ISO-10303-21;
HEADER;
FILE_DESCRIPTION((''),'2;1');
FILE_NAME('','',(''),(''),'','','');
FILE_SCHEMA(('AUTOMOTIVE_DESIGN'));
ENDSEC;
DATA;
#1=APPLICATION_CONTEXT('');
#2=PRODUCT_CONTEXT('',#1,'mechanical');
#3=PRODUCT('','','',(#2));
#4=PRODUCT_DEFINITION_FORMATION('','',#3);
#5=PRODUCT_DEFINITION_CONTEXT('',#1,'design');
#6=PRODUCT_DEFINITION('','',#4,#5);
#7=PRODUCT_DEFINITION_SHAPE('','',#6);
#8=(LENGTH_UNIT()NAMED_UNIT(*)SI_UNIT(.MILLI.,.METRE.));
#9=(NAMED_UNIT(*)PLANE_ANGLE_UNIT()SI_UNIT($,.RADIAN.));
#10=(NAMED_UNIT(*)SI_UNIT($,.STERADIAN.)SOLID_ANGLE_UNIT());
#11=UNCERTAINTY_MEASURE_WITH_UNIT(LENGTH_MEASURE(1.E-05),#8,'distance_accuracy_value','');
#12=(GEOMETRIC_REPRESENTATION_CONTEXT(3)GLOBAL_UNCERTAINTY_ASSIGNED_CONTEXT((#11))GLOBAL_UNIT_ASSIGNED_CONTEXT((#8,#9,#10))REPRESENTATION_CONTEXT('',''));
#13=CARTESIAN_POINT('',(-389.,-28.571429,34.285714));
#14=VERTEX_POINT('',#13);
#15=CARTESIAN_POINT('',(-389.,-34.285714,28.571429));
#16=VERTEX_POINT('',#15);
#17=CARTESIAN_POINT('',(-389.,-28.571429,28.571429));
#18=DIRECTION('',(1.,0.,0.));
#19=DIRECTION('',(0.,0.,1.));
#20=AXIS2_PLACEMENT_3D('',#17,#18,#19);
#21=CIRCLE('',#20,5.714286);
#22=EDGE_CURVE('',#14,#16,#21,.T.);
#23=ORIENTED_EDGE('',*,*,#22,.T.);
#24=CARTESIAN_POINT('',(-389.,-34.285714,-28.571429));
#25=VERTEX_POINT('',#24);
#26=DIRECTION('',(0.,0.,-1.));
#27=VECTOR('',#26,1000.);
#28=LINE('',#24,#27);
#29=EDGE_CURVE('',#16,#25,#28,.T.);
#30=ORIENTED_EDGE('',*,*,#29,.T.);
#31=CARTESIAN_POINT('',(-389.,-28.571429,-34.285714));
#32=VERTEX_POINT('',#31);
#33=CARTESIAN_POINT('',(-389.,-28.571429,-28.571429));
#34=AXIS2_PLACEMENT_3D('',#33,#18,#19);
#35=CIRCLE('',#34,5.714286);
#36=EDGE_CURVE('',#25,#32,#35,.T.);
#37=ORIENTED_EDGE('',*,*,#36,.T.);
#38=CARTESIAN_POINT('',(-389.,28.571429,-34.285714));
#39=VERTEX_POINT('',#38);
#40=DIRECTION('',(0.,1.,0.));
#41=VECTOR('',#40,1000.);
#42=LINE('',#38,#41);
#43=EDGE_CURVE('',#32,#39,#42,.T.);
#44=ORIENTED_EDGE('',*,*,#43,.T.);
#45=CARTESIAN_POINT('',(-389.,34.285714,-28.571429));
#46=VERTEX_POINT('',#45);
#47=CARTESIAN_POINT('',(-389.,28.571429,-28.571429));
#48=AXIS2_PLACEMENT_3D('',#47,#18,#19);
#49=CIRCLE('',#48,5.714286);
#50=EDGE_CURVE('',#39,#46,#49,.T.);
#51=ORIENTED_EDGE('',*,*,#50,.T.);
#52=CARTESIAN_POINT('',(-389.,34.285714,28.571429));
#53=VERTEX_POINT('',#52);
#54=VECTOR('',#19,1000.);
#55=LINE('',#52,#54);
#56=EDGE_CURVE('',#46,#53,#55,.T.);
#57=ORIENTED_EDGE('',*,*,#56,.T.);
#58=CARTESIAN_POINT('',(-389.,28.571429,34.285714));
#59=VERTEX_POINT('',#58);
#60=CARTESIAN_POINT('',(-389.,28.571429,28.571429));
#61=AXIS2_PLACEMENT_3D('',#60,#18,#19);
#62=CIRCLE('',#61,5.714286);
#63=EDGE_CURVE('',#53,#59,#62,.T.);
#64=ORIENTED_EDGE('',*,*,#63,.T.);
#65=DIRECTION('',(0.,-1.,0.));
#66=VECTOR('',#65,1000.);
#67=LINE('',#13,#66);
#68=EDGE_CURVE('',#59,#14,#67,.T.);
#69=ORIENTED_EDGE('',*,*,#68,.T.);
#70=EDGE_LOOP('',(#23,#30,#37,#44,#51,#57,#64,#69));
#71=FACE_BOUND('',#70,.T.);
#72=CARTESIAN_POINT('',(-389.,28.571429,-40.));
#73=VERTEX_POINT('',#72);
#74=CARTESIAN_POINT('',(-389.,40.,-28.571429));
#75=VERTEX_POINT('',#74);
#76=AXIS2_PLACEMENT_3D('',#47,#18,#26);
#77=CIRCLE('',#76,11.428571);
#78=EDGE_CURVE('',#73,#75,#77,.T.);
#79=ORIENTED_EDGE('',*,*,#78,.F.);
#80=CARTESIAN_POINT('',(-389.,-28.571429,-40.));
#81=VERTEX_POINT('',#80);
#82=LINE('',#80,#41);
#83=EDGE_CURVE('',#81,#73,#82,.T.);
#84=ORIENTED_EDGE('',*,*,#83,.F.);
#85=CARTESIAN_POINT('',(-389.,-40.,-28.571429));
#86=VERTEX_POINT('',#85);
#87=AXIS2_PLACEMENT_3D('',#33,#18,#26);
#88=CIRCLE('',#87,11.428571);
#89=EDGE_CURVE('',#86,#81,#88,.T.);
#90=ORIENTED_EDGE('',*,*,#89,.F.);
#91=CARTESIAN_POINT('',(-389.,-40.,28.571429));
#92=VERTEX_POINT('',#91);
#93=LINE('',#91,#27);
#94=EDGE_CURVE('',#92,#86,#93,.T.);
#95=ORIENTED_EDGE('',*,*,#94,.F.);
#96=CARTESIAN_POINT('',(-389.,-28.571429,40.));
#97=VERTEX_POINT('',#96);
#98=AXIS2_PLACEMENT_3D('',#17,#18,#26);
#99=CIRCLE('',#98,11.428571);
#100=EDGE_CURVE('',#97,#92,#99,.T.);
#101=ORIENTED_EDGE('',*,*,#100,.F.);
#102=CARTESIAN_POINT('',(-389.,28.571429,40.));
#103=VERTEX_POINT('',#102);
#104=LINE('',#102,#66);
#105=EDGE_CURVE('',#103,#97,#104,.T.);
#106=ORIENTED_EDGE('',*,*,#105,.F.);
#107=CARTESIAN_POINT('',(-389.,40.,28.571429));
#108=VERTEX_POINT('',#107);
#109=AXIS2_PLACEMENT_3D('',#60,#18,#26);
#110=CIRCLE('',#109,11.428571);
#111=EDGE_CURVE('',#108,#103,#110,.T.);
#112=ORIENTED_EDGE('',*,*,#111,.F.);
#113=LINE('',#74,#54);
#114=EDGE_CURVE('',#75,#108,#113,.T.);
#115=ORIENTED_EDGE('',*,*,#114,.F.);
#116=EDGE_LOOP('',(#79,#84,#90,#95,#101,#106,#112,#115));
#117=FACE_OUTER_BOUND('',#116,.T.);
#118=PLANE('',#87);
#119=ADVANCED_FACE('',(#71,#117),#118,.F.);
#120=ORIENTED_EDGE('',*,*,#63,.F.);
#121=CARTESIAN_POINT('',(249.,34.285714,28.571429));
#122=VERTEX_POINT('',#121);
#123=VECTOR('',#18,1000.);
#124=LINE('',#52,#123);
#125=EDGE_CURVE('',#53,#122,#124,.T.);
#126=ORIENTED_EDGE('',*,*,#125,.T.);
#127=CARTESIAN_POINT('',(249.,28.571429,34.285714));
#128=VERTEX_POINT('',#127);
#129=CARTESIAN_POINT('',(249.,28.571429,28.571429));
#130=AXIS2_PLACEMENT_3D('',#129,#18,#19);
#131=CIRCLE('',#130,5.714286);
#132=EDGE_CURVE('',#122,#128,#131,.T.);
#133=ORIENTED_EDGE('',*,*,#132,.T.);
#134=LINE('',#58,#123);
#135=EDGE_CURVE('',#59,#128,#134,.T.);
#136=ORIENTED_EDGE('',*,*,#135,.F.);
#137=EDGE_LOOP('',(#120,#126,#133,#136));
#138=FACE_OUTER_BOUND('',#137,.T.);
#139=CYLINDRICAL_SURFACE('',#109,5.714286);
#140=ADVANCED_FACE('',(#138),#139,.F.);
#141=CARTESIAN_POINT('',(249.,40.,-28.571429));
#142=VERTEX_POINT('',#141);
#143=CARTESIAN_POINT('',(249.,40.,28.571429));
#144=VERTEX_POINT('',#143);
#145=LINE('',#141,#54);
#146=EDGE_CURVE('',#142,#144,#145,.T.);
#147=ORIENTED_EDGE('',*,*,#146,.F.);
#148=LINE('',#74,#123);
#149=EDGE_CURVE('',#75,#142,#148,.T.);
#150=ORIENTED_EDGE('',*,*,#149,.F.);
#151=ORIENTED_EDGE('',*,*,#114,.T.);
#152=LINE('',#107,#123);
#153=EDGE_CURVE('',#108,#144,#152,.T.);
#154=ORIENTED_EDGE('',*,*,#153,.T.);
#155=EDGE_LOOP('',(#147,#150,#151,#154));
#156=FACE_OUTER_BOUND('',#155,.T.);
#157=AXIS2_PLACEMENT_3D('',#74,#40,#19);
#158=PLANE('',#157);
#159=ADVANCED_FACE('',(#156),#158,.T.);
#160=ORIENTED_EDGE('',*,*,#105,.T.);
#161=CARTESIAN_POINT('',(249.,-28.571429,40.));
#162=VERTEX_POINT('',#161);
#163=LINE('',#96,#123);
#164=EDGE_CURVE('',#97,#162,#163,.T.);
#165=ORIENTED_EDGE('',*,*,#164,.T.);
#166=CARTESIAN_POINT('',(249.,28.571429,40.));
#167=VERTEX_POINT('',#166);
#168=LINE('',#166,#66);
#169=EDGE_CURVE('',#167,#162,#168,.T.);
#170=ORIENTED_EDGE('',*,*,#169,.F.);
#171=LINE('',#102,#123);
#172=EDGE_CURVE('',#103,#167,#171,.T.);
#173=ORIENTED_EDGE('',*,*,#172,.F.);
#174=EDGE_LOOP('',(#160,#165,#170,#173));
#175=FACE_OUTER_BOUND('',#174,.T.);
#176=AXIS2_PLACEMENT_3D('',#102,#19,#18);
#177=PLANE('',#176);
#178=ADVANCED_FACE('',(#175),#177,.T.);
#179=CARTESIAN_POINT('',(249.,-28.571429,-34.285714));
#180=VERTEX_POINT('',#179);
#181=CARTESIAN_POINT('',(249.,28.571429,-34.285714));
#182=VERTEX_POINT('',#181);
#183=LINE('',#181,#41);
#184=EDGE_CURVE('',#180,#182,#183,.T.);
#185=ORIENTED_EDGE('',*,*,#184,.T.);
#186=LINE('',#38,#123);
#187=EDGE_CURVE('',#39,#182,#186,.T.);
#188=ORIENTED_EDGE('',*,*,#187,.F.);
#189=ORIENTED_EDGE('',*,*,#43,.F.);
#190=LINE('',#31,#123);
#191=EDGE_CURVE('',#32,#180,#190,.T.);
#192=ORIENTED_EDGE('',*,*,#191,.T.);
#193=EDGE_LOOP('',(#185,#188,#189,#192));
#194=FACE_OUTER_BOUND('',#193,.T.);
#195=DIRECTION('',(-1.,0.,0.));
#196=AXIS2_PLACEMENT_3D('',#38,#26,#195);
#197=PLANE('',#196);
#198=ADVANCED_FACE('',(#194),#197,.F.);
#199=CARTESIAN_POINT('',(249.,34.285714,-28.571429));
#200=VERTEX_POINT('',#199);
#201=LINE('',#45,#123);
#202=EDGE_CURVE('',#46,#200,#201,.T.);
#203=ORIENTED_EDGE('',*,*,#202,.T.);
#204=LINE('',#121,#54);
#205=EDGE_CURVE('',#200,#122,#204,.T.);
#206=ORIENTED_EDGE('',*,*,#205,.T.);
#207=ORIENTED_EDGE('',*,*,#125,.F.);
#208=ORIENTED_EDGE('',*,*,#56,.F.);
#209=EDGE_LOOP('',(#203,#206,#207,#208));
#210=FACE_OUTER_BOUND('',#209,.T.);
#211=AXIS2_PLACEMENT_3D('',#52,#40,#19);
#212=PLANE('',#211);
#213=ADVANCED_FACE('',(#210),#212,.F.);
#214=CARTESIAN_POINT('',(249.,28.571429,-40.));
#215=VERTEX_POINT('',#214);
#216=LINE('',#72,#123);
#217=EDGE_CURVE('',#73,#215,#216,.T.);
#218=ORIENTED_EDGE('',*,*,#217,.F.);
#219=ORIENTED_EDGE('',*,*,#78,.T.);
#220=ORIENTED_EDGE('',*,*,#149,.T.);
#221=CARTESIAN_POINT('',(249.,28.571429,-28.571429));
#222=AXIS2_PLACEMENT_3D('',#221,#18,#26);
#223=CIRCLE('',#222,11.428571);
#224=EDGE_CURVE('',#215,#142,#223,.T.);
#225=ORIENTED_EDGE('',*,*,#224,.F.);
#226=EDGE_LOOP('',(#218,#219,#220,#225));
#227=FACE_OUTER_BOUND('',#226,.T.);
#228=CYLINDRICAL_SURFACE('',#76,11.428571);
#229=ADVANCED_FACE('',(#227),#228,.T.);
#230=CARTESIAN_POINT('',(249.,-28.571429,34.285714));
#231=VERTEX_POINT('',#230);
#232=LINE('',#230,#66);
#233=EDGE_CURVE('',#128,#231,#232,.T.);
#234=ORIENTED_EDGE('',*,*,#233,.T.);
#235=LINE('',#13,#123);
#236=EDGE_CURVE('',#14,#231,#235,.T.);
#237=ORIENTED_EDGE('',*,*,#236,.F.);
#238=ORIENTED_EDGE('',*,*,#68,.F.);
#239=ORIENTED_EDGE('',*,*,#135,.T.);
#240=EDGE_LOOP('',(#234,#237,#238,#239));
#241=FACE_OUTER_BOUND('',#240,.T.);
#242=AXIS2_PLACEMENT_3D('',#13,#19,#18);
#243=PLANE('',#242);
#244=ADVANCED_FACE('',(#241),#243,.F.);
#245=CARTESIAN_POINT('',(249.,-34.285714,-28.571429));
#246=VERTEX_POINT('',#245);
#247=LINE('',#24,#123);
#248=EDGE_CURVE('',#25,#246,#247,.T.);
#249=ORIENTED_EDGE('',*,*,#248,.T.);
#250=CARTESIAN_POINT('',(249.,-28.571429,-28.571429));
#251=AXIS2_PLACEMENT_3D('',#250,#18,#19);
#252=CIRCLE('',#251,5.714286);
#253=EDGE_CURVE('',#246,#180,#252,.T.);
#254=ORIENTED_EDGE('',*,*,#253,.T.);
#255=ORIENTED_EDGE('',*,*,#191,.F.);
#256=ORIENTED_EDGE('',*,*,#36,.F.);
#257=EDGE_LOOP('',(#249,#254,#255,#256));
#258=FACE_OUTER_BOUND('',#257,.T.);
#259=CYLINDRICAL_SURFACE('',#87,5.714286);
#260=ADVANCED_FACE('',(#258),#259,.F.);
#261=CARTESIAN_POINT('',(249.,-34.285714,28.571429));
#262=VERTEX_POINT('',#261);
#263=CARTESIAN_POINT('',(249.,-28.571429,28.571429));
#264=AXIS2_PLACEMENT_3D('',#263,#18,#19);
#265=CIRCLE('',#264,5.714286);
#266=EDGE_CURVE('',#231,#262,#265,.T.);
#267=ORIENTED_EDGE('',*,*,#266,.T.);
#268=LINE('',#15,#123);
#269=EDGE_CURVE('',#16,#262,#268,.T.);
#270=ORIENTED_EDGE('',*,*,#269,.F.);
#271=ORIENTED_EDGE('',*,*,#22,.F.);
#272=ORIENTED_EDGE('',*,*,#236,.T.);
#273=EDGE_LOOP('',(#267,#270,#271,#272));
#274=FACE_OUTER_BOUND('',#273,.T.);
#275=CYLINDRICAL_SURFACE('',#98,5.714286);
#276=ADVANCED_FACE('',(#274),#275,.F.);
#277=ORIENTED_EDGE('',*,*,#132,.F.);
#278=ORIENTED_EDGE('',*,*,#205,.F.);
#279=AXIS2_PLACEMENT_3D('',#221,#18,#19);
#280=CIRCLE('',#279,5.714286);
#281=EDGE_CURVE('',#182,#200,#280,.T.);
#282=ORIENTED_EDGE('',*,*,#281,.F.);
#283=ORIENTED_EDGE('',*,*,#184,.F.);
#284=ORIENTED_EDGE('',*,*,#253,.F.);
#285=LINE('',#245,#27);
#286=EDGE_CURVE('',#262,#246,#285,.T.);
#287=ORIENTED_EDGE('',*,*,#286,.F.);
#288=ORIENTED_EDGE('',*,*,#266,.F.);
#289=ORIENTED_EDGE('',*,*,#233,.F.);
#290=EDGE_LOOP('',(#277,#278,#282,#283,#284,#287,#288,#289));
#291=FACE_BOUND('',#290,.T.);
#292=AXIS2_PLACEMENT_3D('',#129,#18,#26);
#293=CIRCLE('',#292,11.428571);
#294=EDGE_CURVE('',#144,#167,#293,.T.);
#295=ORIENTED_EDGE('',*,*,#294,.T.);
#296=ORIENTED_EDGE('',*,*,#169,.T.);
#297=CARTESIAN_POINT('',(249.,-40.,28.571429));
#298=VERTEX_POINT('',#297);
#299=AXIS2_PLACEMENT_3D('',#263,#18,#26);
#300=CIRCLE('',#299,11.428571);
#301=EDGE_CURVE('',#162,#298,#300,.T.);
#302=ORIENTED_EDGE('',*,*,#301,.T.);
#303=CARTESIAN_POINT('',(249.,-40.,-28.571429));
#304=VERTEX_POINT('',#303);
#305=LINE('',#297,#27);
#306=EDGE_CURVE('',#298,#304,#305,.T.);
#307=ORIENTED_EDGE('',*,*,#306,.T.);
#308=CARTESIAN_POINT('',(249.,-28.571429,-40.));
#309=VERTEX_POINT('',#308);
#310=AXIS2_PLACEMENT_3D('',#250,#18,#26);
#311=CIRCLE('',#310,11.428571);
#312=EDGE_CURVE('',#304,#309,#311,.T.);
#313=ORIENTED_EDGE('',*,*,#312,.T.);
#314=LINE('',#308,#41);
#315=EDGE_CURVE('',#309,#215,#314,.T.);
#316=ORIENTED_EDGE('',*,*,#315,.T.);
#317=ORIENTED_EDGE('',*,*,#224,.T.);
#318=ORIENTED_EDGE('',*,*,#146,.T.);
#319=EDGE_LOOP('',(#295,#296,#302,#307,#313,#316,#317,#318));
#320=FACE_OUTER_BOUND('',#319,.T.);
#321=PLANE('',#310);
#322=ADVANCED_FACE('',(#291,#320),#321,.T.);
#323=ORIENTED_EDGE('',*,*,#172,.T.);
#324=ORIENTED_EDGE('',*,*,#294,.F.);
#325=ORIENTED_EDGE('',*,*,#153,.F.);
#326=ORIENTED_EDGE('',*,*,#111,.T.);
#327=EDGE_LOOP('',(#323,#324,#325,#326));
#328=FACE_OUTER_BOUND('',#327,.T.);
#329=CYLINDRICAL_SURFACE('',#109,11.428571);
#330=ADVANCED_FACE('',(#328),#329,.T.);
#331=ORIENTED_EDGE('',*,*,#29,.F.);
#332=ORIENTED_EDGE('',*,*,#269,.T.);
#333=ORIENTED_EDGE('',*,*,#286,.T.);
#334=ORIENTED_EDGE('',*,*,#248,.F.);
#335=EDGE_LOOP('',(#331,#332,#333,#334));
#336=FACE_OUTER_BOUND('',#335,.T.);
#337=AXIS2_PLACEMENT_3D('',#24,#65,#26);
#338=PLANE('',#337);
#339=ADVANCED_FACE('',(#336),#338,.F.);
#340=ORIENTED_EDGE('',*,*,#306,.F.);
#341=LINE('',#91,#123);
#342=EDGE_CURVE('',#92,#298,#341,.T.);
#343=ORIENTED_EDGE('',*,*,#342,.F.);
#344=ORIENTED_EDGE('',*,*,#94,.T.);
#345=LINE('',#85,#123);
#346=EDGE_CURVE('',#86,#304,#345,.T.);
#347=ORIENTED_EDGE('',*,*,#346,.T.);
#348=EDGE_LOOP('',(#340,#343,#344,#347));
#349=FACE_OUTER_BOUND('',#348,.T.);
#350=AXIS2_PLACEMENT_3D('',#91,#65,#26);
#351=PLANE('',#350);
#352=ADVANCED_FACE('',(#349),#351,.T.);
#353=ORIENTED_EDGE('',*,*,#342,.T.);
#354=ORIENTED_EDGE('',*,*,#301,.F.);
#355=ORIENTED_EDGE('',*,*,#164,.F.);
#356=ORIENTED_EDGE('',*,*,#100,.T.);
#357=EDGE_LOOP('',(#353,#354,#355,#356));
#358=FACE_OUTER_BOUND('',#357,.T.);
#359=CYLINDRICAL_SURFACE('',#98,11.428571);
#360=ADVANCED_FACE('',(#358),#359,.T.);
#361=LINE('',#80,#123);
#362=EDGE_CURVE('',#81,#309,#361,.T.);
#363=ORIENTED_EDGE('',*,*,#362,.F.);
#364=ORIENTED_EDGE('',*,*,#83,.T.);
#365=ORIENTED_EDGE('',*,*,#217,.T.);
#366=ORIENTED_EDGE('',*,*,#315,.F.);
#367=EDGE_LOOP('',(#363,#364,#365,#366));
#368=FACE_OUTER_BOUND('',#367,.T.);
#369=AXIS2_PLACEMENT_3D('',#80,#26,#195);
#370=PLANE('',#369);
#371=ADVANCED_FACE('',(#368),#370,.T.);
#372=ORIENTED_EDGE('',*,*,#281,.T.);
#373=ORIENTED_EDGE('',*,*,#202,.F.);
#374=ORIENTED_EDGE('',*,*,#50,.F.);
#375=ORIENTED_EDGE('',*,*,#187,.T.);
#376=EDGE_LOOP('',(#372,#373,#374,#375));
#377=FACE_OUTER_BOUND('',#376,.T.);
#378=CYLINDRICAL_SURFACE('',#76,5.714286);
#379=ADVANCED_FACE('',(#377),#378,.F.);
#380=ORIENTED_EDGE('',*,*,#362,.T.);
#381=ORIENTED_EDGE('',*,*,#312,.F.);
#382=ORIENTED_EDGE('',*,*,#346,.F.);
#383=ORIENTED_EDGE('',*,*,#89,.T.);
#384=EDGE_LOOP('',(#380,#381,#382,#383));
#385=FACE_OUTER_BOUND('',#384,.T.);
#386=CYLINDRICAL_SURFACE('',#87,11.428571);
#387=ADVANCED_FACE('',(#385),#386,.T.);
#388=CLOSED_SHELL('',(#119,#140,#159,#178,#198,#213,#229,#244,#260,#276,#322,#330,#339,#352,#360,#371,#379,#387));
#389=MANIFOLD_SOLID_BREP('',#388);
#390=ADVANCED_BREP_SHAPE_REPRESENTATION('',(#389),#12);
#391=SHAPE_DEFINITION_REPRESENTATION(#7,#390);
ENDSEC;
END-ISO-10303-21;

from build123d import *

# Parameters (mm, degrees)
BOSS_EXTRUDE1_DEPTH = 638


with BuildPart() as part:
    # Sketch1 → Boss-Extrude1 (new body)
    with BuildSketch(Plane(origin=(249, 0, 0), x_dir=(0, 0, -1), z_dir=(1, 0, 0))):
        with BuildLine():
            Line((40, -28.571428571), (40, 28.571428571))
            ThreePointArc((40, 28.571428571), (36.652648928, 36.652648928), (28.571428571, 40))
            Line((28.571428571, 40), (-28.571428571, 40))
            ThreePointArc((-28.571428571, 40), (-36.652648928, 36.652648928), (-40, 28.571428571))
            Line((-40, 28.571428571), (-40, -28.571428571))
            ThreePointArc((-40, -28.571428571), (-36.652648928, -36.652648928), (-28.571428571, -40))
            Line((-28.571428571, -40), (28.571428571, -40))
            ThreePointArc((28.571428571, -40), (36.652648928, -36.652648928), (40, -28.571428571))
        make_face()
        with BuildLine():
            Line((-34.285714286, -28.571428571), (-34.285714286, 28.571428571))
            ThreePointArc((-34.285714286, 28.571428571), (-32.61203875, 32.61203875), (-28.571428571, 34.285714286))
            Line((-28.571428571, 34.285714286), (28.571428571, 34.285714286))
            ThreePointArc((28.571428571, 34.285714286), (32.61203875, 32.61203875), (34.285714286, 28.571428571))
            Line((34.285714286, 28.571428571), (34.285714286, -28.571428571))
            ThreePointArc((34.285714286, -28.571428571), (32.61203875, -32.61203875), (28.571428571, -34.285714286))
            Line((28.571428571, -34.285714286), (-28.571428571, -34.285714286))
            ThreePointArc((-28.571428571, -34.285714286), (-32.61203875, -32.61203875), (-34.285714286, -28.571428571))
        make_face(mode=Mode.SUBTRACT)
    extrude(amount=-BOSS_EXTRUDE1_DEPTH)


solid = part.part
